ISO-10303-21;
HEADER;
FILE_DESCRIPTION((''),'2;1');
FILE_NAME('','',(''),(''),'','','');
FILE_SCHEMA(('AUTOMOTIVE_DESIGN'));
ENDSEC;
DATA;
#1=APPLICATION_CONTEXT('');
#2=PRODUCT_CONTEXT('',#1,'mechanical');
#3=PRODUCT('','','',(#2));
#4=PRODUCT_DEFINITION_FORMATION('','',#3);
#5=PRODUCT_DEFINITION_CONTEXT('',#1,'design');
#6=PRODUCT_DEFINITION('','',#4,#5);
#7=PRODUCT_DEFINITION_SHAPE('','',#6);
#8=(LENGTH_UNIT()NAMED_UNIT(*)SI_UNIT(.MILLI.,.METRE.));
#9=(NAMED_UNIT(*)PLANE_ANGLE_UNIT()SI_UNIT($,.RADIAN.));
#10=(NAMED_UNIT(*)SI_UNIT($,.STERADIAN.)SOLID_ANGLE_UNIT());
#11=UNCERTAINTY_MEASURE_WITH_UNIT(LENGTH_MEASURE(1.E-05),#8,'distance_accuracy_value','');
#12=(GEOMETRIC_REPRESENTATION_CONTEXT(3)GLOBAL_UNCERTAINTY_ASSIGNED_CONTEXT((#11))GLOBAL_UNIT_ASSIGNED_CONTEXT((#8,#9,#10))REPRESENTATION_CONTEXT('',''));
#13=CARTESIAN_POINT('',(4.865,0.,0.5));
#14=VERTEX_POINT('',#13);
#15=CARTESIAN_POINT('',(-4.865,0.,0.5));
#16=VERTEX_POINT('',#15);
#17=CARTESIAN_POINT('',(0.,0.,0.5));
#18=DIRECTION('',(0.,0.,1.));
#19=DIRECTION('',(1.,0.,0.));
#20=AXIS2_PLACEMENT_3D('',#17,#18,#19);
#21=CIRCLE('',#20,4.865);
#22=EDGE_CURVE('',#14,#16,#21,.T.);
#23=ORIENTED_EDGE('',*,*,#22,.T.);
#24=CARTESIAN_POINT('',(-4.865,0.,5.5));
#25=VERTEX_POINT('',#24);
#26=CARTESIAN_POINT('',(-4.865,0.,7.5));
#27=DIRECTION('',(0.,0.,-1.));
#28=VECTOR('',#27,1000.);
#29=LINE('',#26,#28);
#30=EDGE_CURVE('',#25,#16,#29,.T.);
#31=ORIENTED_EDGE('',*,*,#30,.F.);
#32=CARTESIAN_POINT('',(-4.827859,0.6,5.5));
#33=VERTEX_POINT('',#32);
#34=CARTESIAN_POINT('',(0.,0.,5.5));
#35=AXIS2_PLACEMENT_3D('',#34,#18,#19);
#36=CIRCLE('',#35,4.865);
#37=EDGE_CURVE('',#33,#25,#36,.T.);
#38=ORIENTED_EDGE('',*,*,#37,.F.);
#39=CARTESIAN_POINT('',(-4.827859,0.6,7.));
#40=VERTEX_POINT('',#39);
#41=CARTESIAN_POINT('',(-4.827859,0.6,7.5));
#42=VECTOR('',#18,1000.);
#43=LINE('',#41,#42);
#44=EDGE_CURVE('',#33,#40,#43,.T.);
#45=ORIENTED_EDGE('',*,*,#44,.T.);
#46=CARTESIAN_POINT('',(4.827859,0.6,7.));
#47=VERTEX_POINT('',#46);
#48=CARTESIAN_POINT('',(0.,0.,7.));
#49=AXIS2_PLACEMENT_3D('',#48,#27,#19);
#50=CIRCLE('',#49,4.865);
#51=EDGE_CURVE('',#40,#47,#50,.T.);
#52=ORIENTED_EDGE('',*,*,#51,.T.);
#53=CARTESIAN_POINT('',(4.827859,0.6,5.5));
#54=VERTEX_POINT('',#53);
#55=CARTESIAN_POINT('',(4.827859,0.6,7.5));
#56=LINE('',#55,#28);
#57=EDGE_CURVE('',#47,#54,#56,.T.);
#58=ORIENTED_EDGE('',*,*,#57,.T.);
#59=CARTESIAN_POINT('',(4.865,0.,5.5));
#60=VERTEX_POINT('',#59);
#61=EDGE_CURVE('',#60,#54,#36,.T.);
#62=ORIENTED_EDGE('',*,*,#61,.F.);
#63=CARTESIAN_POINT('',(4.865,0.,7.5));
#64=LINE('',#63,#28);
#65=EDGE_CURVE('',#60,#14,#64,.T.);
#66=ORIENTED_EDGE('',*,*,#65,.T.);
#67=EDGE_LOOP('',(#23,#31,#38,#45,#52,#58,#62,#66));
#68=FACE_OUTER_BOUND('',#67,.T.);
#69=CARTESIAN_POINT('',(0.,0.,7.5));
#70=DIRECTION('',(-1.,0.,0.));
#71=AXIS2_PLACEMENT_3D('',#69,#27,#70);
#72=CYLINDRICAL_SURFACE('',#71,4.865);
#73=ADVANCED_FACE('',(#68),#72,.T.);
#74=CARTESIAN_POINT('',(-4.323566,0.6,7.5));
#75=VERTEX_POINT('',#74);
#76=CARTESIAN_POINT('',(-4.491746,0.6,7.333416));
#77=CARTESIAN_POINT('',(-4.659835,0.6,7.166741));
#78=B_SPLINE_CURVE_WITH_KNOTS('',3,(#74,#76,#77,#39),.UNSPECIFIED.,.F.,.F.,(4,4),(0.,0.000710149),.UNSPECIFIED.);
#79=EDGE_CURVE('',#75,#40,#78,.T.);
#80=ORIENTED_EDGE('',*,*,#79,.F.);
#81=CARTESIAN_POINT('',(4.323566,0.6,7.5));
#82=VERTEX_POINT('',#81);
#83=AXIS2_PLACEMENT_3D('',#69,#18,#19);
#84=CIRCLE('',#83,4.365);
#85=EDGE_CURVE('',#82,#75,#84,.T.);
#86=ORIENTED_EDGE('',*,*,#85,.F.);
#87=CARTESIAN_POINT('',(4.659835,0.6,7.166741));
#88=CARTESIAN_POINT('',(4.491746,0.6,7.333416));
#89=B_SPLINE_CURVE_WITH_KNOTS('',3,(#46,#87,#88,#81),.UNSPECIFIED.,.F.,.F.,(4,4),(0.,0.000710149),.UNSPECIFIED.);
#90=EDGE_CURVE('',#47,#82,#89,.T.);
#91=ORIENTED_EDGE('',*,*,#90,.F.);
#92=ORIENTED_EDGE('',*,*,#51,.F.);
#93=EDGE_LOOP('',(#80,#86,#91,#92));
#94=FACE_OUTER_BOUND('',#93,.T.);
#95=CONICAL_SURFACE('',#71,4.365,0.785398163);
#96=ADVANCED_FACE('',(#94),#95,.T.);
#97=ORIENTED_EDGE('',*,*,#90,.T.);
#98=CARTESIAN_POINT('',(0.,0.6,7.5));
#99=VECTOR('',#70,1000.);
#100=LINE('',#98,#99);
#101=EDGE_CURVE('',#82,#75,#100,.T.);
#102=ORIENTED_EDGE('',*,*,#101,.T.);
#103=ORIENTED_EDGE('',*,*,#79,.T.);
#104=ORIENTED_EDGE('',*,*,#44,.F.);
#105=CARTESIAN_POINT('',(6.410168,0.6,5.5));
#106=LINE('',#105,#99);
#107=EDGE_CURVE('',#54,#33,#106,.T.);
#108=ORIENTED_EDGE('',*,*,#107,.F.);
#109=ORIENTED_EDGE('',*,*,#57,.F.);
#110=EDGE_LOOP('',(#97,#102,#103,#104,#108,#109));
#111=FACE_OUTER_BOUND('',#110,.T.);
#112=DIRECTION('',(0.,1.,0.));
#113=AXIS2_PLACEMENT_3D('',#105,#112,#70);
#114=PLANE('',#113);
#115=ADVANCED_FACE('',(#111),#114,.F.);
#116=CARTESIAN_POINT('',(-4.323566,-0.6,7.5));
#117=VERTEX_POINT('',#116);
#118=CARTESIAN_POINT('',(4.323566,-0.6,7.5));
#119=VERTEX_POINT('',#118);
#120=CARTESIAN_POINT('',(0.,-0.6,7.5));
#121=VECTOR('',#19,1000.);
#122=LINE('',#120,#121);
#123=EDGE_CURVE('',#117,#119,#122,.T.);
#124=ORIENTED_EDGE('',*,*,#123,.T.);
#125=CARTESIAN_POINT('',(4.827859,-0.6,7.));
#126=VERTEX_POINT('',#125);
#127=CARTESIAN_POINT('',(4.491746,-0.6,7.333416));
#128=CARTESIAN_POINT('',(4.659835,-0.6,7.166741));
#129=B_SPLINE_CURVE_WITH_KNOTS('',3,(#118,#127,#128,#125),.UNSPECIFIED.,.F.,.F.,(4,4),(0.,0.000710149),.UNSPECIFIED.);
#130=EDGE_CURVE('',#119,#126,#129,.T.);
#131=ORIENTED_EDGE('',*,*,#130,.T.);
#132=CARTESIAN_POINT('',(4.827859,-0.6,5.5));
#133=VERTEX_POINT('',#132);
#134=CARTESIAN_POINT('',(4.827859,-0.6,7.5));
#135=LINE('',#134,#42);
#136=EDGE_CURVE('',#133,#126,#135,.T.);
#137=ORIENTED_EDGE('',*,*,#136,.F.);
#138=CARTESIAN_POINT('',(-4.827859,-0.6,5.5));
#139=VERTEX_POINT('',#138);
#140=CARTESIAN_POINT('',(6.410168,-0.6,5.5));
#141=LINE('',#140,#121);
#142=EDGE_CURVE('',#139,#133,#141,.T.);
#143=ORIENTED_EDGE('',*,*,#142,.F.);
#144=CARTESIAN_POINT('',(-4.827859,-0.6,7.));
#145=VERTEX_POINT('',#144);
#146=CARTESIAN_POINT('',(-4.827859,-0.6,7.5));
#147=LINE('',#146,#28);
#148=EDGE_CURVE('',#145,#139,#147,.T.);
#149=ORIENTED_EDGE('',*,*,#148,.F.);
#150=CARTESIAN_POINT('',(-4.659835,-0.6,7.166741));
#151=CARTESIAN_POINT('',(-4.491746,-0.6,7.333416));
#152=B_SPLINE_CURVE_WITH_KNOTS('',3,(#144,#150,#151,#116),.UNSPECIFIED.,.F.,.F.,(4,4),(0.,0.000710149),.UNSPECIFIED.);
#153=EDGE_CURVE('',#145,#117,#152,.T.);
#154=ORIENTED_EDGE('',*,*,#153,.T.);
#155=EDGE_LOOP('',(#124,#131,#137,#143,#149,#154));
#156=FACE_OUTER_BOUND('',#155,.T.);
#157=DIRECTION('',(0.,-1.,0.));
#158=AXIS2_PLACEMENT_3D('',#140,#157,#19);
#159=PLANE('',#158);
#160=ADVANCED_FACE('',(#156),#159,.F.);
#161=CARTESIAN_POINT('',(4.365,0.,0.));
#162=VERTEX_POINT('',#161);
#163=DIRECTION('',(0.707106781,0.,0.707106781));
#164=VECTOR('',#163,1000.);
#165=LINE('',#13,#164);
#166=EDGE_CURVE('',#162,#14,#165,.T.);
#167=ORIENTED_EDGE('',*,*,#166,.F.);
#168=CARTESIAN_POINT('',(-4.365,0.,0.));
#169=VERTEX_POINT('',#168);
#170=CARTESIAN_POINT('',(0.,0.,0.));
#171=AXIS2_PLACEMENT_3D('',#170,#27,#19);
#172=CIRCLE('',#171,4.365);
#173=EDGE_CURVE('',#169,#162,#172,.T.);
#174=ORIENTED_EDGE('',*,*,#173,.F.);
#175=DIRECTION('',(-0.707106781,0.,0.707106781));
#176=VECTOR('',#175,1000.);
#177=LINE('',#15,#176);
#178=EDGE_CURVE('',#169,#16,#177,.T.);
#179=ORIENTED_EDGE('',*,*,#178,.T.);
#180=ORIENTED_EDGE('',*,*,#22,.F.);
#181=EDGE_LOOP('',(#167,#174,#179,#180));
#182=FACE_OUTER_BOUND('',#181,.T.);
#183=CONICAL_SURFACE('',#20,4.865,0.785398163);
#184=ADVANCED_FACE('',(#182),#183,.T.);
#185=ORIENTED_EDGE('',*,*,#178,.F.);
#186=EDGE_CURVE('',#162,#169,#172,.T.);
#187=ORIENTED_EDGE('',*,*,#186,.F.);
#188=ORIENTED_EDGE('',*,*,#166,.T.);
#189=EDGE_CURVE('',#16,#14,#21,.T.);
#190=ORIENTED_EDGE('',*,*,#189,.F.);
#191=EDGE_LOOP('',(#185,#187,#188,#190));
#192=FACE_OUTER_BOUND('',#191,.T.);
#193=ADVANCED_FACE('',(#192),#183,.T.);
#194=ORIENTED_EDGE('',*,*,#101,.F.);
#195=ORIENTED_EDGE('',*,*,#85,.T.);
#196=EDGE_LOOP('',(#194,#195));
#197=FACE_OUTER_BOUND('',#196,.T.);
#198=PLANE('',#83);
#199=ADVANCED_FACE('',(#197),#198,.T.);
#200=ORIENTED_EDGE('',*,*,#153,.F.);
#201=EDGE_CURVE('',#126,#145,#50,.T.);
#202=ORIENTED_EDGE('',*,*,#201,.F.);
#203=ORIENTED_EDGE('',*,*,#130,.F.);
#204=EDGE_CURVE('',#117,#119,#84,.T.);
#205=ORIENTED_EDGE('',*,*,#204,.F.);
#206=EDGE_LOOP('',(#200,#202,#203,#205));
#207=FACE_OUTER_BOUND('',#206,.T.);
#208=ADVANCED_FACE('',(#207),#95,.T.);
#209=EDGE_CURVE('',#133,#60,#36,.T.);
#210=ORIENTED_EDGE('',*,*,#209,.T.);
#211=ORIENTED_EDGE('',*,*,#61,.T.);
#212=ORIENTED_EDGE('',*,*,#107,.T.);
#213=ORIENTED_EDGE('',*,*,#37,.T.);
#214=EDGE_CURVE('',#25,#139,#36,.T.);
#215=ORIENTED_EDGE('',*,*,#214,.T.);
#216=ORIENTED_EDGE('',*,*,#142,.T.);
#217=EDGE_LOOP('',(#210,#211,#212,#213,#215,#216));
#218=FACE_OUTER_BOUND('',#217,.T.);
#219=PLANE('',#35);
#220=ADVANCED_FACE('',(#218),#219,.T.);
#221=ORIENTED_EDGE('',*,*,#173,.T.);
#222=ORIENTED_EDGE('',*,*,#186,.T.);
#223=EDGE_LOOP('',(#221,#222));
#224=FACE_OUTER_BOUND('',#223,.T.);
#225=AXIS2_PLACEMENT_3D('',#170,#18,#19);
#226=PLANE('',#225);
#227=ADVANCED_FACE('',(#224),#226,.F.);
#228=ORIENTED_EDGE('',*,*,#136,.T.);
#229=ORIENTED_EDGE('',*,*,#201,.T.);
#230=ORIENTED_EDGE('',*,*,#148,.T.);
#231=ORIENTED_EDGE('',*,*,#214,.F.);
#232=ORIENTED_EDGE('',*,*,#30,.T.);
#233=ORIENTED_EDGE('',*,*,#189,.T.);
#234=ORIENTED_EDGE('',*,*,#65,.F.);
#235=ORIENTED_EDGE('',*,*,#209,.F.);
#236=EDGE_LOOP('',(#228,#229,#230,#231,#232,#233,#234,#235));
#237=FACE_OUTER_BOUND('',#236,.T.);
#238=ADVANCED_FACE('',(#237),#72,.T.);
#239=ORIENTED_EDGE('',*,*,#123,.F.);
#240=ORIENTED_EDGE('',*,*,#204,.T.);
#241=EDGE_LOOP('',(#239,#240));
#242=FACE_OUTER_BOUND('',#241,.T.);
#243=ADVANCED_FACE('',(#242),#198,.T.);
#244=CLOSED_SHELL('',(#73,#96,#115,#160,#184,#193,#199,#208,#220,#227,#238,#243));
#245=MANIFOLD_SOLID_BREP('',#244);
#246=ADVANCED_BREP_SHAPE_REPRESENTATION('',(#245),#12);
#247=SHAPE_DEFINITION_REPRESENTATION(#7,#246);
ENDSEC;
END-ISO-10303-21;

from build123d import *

# Parameters (mm, degrees)
SKETCH1_R           = 4.865
BOSS_EXTRUDE1_DEPTH = 7.5
SKETCH2_W           = 12.82033658
SKETCH2_H           = 1.2
CUT_EXTRUDE1_DEPTH  = 2
CHAMFER1_SIZE       = 0.5


with BuildPart() as part:
    # Sketch1 → Boss-Extrude1 (new body)
    with BuildSketch(Plane.XY):
        Circle(SKETCH1_R)
    extrude(amount=BOSS_EXTRUDE1_DEPTH)

    # Sketch2 → Cut-Extrude1 (cut)
    with BuildSketch(Plane.XY.offset(7.5)):
        Rectangle(SKETCH2_W, SKETCH2_H)
    extrude(amount=-CUT_EXTRUDE1_DEPTH, mode=Mode.SUBTRACT)

    # Chamfer1
    chamfer1_edges = [part.edges().sort_by_distance(p)[0] for p in [
        (-4.865, 0, 0),
        (0, 4.865, 7.5),
        (0, -4.865, 7.5),
    ]]
    chamfer(chamfer1_edges, length=CHAMFER1_SIZE)


solid = part.part
